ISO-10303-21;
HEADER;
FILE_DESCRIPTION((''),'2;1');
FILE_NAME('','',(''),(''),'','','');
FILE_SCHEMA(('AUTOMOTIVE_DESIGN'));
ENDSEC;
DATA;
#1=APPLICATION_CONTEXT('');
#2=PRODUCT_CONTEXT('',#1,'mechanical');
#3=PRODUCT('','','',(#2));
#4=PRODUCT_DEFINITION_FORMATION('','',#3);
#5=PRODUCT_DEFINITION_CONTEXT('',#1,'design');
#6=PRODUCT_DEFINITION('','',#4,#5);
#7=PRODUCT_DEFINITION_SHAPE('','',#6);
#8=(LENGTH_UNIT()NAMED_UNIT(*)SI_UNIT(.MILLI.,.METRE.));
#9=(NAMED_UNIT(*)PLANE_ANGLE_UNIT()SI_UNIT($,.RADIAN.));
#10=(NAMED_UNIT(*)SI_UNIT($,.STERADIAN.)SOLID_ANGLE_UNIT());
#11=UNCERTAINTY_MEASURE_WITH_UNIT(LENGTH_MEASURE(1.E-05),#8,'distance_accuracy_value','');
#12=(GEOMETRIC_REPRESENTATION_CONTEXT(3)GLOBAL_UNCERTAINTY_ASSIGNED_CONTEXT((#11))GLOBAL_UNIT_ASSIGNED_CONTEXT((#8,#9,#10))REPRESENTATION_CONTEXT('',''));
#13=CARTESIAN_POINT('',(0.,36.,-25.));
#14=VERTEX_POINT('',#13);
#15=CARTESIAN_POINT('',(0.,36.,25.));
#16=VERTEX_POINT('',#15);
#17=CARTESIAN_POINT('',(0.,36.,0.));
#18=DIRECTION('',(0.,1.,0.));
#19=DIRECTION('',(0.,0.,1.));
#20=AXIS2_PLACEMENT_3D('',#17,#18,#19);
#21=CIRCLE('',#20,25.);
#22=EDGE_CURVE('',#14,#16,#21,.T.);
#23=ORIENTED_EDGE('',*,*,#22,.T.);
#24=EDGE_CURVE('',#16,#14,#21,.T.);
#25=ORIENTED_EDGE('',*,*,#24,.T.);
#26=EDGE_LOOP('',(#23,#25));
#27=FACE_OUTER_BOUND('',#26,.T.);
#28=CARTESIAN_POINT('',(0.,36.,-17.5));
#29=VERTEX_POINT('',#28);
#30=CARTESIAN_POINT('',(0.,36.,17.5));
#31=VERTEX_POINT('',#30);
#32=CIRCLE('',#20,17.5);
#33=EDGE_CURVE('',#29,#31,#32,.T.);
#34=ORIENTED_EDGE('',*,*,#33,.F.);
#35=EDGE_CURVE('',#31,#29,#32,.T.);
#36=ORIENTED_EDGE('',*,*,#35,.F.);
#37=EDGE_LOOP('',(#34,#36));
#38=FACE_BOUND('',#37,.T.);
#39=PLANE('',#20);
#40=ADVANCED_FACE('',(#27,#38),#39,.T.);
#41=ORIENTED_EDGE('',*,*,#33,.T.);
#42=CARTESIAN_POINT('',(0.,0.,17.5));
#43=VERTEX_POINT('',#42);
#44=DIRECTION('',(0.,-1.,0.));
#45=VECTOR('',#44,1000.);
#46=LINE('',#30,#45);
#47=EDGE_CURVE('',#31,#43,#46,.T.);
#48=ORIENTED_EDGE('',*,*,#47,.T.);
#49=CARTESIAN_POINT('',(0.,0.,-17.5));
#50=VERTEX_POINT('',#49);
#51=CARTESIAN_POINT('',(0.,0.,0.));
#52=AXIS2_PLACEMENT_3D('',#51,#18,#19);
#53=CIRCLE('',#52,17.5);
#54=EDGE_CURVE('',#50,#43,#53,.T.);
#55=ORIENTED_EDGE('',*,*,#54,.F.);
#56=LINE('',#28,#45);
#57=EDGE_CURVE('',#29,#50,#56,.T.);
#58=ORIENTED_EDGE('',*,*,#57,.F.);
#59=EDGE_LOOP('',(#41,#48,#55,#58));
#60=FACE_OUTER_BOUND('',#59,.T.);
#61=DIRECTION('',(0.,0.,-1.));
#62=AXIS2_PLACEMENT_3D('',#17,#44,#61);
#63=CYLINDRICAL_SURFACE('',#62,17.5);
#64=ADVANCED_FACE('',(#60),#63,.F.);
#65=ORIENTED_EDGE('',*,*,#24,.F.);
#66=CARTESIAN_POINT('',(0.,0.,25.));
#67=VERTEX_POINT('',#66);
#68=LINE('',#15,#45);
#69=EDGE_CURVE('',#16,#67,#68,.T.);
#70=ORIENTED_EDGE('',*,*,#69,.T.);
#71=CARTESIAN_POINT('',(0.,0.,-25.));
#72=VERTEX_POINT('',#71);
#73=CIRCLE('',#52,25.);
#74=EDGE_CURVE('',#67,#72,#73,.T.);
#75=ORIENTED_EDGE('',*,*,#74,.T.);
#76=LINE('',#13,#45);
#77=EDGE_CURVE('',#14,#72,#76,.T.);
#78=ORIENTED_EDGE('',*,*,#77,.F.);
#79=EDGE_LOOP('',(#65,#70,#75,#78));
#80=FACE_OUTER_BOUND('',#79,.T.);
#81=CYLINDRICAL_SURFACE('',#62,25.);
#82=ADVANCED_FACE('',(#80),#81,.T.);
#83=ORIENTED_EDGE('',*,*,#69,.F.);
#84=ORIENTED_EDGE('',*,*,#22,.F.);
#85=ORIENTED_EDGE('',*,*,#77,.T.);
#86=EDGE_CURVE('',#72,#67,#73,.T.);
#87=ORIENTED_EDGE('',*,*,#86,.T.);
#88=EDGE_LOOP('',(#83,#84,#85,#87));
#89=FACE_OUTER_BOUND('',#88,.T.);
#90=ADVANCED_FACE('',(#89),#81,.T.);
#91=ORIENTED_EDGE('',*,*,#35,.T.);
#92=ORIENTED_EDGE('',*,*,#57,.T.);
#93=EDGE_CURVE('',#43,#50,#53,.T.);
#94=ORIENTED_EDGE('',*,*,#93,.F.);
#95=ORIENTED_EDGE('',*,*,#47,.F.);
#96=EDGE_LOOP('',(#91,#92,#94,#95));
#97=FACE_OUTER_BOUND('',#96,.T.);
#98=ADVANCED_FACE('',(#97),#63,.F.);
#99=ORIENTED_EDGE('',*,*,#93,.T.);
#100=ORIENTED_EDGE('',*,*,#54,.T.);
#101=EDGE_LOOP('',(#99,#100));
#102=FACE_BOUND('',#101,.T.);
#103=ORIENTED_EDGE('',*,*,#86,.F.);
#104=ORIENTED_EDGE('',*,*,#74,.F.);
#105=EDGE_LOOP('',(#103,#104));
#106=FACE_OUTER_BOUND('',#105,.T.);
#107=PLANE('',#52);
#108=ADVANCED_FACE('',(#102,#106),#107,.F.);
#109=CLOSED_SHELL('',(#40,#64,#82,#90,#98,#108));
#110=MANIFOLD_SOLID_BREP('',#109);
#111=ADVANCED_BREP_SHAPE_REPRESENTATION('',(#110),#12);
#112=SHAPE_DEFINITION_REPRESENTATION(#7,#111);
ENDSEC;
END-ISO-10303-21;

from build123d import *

# Parameters (mm, degrees)
SKETCH1_R           = 25
SKETCH1_R_2         = 17.5
BOSS_EXTRUDE1_DEPTH = 36


with BuildPart() as part:
    # Sketch1 → Boss-Extrude1 (new body)
    with BuildSketch(Plane(origin=(0, 0, 0), x_dir=(1, 0, 0), z_dir=(0, 1, 0))):
        with Locations(Location((0, 0, 0), (0, 0, 270))):
            Circle(SKETCH1_R)
        with Locations(Location((0, 0, 0), (0, 0, 270))):
            Circle(SKETCH1_R_2, mode=Mode.SUBTRACT)
    extrude(amount=BOSS_EXTRUDE1_DEPTH)


solid = part.part
